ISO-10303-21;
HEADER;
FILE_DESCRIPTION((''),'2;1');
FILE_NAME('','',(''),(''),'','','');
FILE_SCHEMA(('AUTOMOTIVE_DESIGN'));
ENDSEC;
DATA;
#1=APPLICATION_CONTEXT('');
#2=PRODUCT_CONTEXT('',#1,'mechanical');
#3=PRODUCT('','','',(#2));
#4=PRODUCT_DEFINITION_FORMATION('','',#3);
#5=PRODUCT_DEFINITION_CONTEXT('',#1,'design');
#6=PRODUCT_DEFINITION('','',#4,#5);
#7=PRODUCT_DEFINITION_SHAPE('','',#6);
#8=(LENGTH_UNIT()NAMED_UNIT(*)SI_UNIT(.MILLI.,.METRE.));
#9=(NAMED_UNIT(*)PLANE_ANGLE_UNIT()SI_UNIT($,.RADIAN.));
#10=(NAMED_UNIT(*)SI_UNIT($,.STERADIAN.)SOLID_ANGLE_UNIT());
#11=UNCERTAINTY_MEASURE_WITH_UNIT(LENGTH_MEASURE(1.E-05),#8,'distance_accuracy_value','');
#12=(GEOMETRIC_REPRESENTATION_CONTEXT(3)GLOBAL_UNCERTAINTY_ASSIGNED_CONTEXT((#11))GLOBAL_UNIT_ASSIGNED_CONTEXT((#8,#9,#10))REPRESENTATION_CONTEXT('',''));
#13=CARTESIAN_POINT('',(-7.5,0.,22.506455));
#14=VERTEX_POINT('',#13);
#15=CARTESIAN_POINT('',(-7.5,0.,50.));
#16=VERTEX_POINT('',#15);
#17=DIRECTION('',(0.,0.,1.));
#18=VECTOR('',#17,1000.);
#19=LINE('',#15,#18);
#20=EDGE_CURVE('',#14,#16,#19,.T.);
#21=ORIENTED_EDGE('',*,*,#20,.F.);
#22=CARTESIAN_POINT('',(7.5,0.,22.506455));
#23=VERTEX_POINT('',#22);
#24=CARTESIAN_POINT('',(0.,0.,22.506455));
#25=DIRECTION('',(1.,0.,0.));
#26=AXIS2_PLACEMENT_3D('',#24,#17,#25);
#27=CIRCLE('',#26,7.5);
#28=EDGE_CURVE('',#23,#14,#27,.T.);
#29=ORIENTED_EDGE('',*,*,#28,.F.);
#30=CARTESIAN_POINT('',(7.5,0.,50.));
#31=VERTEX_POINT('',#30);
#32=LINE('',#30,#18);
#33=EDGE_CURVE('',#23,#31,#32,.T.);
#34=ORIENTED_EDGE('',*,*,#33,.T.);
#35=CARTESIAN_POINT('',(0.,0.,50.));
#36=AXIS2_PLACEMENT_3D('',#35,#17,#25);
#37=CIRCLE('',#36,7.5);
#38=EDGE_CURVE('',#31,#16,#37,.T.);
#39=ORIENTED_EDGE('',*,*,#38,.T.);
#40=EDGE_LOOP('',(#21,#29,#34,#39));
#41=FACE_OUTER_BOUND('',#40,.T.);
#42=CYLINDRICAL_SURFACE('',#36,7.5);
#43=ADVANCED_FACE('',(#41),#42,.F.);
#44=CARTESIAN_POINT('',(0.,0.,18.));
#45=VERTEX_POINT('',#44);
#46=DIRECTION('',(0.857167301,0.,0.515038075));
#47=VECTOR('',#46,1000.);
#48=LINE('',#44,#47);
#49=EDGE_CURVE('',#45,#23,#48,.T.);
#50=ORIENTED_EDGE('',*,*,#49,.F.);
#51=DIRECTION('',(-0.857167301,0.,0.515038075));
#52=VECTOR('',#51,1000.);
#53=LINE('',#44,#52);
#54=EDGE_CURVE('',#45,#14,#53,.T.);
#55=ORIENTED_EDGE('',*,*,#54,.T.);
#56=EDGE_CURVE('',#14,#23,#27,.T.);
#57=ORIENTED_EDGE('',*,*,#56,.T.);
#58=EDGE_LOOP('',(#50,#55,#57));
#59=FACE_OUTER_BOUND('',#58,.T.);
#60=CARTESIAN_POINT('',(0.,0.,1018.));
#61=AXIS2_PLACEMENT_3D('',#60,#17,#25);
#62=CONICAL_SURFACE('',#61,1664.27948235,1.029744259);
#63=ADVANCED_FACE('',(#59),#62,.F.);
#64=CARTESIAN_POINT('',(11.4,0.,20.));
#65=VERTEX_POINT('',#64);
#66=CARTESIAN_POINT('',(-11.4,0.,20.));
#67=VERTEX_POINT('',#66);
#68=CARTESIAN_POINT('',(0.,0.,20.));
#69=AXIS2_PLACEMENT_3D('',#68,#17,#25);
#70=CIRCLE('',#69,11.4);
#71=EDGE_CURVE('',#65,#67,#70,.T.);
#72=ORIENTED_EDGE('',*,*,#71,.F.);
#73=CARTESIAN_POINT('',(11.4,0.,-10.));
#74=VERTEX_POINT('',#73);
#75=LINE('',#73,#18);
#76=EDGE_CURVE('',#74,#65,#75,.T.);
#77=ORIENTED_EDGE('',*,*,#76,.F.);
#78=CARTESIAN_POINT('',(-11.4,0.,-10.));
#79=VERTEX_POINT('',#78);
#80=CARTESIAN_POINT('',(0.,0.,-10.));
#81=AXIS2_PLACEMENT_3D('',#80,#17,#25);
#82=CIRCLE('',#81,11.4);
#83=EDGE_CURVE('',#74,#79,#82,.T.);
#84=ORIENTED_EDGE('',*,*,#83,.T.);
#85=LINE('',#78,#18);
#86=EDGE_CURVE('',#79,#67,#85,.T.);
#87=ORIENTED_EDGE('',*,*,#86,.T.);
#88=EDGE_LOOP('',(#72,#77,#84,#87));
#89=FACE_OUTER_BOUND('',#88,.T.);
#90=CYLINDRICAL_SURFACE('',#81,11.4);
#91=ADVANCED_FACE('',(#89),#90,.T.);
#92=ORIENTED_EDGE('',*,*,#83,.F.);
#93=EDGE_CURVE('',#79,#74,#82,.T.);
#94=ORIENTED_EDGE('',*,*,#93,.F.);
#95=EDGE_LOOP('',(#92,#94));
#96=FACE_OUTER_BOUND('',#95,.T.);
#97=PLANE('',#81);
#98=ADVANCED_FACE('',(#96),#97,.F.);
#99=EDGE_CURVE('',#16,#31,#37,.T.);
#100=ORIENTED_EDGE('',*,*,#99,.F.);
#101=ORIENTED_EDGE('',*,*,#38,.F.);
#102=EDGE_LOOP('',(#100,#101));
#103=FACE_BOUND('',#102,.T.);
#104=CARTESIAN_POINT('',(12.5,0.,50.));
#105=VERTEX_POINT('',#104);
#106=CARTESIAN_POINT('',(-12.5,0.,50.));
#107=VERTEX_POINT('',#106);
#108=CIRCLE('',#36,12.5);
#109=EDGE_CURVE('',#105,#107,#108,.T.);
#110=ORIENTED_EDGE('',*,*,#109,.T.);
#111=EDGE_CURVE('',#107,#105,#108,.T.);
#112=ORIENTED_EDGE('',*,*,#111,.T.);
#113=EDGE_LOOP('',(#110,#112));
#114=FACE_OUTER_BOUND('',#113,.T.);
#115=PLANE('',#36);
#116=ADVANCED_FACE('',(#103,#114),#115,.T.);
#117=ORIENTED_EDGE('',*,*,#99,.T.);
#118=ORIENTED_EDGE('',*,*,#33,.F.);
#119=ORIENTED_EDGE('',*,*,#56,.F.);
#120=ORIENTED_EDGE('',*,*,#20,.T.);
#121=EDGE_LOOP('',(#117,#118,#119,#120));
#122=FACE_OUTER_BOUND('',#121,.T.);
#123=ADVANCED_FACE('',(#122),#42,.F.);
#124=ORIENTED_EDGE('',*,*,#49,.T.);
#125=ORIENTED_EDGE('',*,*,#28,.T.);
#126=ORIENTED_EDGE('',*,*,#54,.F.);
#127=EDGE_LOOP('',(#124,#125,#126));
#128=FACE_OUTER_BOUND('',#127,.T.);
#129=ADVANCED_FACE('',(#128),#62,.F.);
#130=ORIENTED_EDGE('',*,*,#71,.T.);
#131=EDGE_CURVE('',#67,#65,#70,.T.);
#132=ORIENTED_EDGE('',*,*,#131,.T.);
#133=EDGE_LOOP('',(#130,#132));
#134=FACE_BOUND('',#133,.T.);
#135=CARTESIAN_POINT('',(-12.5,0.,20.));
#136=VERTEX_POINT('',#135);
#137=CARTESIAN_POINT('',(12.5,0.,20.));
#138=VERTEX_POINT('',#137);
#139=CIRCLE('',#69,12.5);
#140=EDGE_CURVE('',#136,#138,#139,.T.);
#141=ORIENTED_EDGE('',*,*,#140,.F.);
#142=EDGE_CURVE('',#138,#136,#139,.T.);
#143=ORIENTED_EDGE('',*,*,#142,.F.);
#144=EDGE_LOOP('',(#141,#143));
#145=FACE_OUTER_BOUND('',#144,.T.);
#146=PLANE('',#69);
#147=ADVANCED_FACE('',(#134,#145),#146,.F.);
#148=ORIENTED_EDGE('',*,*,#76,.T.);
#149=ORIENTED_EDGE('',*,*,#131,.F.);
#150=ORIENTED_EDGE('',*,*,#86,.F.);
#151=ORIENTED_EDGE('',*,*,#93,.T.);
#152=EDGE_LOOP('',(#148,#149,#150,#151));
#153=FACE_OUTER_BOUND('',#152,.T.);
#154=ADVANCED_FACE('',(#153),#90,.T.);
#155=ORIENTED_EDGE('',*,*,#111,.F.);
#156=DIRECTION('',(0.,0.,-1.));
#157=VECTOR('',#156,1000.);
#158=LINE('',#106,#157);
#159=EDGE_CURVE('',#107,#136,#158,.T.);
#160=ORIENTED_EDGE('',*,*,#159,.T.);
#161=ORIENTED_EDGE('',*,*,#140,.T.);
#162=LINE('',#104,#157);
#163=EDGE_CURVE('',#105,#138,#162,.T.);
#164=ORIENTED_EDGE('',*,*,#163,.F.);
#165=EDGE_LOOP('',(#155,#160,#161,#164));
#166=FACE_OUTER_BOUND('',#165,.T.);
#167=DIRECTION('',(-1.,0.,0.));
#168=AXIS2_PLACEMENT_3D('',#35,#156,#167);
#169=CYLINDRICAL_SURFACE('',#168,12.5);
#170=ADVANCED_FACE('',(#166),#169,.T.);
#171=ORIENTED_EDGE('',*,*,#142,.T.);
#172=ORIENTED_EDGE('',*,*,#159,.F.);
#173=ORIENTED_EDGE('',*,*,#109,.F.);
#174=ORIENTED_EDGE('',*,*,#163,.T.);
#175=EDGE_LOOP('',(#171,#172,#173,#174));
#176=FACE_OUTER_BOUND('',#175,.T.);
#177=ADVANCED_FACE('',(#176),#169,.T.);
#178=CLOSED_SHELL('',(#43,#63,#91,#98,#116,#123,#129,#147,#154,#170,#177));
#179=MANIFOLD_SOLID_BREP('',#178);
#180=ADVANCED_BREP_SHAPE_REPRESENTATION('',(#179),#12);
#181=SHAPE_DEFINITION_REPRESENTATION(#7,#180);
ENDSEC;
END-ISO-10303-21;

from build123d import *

# Parameters (mm, degrees)
EXTRUDE_1_DEPTH      = 20
EXTRUDE_1_DEPTH_BACK = 10
SKETCH_1_R           = 11.4
SKETCH_2_R           = 12.5
EXTRUDE_2_DEPTH      = 30


with BuildPart() as part:
    # 草图1 → 凸台-拉伸1 (new, two sides: drawn at the far end of the back side and taken through both)
    with BuildSketch(Plane.XY.offset(-EXTRUDE_1_DEPTH_BACK)):
        Circle(SKETCH_1_R)
    extrude(amount=EXTRUDE_1_DEPTH + EXTRUDE_1_DEPTH_BACK)

    # 草图2 → 凸台-拉伸2 (add)
    with BuildSketch(Plane.XY.offset(20)):
        Circle(SKETCH_2_R)
    extrude(amount=EXTRUDE_2_DEPTH)

    # 草图7 → 切除-旋转1 (revolve, cut)
    with BuildSketch(Plane(origin=(0, 0, 0), x_dir=(0, 0, -1), z_dir=(1, 0, 0)), mode=Mode.PRIVATE) as cut_revolve_1_sk:
        Polygon((-50, 0), (-18, 0), (-22.506454643, 7.5), (-50, 7.5), align=None)
    revolve(cut_revolve_1_sk.sketch.rotate(Axis((0, 0, 50), (0, 0, -1)), 90), axis=Axis((0, 0, 50), (0, 0, -1)), mode=Mode.SUBTRACT)


solid = part.part
